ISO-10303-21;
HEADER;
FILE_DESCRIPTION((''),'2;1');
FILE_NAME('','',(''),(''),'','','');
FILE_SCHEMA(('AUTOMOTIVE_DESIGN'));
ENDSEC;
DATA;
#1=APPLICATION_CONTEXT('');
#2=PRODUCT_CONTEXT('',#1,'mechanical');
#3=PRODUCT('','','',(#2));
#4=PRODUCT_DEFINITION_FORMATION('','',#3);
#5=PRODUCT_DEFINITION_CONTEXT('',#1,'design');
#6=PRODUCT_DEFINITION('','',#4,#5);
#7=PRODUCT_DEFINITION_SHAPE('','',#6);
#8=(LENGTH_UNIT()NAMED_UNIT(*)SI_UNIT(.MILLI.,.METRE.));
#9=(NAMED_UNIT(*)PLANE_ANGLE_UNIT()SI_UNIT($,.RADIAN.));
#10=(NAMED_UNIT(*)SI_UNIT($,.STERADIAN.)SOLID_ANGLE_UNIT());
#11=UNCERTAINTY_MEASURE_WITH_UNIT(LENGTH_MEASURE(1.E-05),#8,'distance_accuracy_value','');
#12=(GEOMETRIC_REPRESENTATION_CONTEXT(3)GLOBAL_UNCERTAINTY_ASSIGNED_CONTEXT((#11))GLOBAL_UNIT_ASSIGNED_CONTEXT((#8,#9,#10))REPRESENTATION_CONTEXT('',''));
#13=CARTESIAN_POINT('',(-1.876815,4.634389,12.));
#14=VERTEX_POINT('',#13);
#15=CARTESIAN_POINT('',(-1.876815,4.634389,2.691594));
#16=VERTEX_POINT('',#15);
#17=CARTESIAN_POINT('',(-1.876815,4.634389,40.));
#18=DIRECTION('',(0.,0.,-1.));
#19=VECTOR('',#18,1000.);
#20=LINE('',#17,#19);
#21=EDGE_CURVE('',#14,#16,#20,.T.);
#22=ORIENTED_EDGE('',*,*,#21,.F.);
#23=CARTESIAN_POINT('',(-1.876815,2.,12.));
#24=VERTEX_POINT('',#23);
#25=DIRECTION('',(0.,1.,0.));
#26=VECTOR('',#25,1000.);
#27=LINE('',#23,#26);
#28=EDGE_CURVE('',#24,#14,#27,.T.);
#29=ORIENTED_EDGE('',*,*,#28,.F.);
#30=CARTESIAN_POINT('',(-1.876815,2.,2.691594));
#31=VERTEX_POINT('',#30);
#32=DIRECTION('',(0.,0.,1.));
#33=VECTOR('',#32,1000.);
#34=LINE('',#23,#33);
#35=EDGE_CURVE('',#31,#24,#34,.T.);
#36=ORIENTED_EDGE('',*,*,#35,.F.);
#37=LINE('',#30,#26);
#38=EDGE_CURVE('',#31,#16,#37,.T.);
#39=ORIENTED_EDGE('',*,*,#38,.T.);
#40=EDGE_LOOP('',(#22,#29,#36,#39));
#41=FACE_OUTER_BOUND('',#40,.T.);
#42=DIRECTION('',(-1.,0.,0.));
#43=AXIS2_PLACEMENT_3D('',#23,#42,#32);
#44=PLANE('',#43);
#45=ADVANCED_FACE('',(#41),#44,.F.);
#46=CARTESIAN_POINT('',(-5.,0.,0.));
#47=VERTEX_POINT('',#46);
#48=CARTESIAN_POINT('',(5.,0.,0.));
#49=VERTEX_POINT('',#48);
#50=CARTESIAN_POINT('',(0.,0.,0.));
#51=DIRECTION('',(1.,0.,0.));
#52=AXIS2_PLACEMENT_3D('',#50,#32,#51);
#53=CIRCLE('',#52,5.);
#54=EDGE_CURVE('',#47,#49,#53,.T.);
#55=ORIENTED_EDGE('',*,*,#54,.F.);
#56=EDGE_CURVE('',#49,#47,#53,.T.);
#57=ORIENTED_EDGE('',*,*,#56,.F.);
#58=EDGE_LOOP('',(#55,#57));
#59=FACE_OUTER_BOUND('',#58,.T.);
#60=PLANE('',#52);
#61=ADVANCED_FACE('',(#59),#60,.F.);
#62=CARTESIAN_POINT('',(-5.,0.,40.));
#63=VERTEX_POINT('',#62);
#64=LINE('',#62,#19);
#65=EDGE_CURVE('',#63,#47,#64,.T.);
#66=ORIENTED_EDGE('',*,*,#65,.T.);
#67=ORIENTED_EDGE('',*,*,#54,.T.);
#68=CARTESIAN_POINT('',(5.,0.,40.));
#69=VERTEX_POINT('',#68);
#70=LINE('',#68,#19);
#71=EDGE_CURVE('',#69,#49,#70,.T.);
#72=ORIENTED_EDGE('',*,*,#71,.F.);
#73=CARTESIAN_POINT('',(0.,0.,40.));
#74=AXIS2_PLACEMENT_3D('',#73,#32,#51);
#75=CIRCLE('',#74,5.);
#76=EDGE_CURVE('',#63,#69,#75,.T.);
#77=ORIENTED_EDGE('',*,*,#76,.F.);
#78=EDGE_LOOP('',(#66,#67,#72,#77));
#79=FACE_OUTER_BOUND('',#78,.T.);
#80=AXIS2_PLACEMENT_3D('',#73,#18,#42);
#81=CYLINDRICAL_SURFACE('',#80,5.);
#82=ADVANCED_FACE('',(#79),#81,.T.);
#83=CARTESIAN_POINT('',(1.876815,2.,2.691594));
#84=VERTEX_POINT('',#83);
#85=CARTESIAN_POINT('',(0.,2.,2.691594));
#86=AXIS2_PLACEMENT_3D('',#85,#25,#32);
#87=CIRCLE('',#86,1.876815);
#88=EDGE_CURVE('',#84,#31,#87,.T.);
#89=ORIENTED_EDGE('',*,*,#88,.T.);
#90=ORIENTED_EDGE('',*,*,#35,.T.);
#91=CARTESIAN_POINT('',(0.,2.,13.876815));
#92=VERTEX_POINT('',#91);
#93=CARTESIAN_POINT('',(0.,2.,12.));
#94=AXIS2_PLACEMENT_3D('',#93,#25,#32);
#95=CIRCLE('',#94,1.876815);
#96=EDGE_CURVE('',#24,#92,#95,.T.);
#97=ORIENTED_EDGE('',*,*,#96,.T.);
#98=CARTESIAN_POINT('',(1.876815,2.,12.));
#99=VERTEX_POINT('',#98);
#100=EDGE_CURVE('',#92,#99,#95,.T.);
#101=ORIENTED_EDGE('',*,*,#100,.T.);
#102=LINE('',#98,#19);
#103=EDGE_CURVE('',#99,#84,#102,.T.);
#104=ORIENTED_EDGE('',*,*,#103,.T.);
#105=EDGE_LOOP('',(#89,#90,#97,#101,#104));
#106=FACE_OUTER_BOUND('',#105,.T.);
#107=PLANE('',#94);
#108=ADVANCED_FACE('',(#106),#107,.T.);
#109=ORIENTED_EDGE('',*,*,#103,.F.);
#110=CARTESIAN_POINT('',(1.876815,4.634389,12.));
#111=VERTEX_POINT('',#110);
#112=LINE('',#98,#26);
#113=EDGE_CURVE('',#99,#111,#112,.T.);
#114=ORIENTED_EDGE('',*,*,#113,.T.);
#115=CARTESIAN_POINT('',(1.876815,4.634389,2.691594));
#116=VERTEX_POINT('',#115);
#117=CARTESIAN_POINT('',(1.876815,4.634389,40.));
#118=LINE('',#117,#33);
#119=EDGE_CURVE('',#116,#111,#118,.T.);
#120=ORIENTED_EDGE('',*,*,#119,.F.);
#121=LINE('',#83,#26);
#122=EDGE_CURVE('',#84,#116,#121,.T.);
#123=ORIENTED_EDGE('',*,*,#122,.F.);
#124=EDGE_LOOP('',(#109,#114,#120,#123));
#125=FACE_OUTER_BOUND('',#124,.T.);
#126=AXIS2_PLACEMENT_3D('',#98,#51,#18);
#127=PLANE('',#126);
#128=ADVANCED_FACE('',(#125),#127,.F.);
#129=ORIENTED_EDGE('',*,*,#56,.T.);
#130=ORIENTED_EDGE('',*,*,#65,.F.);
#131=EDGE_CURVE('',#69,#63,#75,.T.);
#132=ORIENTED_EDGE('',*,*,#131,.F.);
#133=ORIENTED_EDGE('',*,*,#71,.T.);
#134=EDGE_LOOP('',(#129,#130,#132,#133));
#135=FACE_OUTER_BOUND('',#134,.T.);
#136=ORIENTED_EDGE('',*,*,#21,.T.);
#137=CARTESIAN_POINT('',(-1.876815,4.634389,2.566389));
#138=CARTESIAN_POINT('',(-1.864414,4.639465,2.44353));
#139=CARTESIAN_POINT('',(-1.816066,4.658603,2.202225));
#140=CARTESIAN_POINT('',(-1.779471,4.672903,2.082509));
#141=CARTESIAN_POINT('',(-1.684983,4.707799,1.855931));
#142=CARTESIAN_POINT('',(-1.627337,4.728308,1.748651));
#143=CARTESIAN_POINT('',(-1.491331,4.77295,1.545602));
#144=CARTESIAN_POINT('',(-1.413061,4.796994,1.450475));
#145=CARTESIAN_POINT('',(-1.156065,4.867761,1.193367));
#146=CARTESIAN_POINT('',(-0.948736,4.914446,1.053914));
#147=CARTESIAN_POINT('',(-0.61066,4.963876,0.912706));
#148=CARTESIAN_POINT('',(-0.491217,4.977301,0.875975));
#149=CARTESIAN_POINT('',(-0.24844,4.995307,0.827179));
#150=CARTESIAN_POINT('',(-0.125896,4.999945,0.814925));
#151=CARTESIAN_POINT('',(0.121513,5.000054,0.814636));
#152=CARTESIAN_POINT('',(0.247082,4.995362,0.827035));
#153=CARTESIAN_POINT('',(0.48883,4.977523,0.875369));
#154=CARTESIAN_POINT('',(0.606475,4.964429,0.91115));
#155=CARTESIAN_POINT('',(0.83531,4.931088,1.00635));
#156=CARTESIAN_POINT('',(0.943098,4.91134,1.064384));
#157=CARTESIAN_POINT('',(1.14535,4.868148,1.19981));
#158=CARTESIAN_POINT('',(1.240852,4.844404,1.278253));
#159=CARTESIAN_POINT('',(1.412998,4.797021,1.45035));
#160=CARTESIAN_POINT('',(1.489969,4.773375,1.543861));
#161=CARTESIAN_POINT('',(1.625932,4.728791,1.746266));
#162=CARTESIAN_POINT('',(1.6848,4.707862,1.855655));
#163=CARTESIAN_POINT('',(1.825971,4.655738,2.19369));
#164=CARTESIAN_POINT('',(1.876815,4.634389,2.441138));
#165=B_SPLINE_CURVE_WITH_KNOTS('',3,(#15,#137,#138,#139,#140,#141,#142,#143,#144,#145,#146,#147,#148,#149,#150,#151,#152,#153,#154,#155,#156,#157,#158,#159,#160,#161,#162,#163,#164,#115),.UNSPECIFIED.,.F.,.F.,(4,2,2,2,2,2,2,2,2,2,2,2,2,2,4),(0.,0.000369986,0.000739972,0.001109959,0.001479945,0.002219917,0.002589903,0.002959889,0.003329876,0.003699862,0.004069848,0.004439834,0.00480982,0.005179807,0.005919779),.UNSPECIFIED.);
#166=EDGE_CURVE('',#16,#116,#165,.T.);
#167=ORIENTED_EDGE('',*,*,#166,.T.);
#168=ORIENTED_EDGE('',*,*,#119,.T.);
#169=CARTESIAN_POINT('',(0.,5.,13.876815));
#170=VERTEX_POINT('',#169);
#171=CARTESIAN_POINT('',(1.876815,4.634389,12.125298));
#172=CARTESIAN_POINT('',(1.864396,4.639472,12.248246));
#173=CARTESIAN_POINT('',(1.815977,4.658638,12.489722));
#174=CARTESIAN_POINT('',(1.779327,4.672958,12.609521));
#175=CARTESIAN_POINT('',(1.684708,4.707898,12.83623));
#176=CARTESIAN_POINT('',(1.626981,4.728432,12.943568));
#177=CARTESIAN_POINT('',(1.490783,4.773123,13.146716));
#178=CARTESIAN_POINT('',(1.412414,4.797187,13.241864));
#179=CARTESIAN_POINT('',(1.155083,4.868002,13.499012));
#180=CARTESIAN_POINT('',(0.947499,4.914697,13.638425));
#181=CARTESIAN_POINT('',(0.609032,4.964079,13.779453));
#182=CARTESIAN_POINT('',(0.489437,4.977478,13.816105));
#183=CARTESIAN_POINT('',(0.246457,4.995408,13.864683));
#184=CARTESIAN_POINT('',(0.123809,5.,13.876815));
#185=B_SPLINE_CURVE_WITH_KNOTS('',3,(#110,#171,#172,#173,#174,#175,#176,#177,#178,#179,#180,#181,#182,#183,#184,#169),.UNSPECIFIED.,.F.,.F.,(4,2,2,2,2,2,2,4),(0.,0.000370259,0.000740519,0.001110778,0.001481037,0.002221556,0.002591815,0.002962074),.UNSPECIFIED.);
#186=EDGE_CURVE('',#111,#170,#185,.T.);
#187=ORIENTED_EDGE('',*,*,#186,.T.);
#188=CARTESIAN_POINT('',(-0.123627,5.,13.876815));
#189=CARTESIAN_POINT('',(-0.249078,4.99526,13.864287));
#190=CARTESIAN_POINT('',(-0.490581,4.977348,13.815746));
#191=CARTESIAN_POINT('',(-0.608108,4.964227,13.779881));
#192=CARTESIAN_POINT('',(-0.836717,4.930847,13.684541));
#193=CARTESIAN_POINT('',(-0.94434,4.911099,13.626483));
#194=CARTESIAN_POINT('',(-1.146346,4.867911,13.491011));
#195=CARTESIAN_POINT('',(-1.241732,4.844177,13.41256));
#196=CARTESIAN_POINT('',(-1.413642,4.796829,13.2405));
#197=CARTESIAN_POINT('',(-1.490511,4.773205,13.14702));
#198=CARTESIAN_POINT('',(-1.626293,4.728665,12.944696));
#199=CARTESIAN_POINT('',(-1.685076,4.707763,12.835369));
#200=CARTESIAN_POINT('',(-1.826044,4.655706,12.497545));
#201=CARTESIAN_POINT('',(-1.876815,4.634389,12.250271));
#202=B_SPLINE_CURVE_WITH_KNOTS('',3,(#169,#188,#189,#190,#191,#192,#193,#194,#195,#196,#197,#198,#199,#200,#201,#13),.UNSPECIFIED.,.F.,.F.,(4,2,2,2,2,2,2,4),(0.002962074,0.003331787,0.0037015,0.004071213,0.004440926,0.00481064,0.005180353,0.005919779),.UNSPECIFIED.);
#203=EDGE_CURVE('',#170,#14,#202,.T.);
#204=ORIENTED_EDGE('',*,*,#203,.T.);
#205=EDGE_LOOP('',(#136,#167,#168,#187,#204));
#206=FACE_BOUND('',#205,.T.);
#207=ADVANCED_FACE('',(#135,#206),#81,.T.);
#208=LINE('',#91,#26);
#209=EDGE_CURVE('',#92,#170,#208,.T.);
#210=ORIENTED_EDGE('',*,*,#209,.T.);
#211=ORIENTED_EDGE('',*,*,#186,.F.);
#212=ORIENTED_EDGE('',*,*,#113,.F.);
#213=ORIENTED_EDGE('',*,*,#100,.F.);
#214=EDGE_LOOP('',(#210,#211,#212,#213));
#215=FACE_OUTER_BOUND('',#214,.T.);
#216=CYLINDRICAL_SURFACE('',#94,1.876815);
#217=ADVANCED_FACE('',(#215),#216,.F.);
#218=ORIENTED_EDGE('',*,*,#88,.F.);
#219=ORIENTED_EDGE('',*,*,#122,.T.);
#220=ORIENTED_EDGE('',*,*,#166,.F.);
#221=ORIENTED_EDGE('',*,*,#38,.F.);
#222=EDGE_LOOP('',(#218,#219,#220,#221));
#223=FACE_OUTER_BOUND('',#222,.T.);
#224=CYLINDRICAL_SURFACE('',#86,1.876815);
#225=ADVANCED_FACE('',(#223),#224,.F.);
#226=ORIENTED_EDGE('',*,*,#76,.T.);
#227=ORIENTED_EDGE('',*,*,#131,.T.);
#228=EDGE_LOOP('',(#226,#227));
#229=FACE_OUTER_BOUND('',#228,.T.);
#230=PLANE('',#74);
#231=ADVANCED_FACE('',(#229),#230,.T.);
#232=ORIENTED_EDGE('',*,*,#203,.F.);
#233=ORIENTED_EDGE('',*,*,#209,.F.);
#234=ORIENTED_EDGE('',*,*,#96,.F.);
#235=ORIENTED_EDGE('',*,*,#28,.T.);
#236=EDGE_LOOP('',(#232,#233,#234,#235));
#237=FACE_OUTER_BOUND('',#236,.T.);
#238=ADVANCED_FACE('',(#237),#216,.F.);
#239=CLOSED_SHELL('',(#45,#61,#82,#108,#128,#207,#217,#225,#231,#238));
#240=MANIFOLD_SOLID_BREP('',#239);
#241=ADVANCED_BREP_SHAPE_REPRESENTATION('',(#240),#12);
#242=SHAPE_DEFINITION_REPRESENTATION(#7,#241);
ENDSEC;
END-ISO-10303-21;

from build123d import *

# Parameters (mm, degrees)
SKETCH1_R           = 5
BOSS_EXTRUDE1_DEPTH = 40
CUT_EXTRUDE1_DEPTH  = 3


with BuildPart() as part:
    # Sketch1 → Boss-Extrude1 (new body)
    with BuildSketch(Plane.XY):
        Circle(SKETCH1_R)
    extrude(amount=BOSS_EXTRUDE1_DEPTH)

    # Sketch2 → Cut-Extrude1 (cut)
    with BuildSketch(Plane(origin=(0, 5, 0), x_dir=(1, 0, 0), z_dir=(0, 1, 0))):
        with BuildLine():
            Line((-1.876815102, -12), (-1.876815102, -2.691594063))
            ThreePointArc((-1.876815102, -2.691594063), (0, -0.814778961), (1.876815102, -2.691594063))
            Line((1.876815102, -2.691594063), (1.876815102, -12))
            ThreePointArc((1.876815102, -12), (0, -13.876815102), (-1.876815102, -12))
        make_face()
    extrude(amount=-CUT_EXTRUDE1_DEPTH, mode=Mode.SUBTRACT)


solid = part.part
